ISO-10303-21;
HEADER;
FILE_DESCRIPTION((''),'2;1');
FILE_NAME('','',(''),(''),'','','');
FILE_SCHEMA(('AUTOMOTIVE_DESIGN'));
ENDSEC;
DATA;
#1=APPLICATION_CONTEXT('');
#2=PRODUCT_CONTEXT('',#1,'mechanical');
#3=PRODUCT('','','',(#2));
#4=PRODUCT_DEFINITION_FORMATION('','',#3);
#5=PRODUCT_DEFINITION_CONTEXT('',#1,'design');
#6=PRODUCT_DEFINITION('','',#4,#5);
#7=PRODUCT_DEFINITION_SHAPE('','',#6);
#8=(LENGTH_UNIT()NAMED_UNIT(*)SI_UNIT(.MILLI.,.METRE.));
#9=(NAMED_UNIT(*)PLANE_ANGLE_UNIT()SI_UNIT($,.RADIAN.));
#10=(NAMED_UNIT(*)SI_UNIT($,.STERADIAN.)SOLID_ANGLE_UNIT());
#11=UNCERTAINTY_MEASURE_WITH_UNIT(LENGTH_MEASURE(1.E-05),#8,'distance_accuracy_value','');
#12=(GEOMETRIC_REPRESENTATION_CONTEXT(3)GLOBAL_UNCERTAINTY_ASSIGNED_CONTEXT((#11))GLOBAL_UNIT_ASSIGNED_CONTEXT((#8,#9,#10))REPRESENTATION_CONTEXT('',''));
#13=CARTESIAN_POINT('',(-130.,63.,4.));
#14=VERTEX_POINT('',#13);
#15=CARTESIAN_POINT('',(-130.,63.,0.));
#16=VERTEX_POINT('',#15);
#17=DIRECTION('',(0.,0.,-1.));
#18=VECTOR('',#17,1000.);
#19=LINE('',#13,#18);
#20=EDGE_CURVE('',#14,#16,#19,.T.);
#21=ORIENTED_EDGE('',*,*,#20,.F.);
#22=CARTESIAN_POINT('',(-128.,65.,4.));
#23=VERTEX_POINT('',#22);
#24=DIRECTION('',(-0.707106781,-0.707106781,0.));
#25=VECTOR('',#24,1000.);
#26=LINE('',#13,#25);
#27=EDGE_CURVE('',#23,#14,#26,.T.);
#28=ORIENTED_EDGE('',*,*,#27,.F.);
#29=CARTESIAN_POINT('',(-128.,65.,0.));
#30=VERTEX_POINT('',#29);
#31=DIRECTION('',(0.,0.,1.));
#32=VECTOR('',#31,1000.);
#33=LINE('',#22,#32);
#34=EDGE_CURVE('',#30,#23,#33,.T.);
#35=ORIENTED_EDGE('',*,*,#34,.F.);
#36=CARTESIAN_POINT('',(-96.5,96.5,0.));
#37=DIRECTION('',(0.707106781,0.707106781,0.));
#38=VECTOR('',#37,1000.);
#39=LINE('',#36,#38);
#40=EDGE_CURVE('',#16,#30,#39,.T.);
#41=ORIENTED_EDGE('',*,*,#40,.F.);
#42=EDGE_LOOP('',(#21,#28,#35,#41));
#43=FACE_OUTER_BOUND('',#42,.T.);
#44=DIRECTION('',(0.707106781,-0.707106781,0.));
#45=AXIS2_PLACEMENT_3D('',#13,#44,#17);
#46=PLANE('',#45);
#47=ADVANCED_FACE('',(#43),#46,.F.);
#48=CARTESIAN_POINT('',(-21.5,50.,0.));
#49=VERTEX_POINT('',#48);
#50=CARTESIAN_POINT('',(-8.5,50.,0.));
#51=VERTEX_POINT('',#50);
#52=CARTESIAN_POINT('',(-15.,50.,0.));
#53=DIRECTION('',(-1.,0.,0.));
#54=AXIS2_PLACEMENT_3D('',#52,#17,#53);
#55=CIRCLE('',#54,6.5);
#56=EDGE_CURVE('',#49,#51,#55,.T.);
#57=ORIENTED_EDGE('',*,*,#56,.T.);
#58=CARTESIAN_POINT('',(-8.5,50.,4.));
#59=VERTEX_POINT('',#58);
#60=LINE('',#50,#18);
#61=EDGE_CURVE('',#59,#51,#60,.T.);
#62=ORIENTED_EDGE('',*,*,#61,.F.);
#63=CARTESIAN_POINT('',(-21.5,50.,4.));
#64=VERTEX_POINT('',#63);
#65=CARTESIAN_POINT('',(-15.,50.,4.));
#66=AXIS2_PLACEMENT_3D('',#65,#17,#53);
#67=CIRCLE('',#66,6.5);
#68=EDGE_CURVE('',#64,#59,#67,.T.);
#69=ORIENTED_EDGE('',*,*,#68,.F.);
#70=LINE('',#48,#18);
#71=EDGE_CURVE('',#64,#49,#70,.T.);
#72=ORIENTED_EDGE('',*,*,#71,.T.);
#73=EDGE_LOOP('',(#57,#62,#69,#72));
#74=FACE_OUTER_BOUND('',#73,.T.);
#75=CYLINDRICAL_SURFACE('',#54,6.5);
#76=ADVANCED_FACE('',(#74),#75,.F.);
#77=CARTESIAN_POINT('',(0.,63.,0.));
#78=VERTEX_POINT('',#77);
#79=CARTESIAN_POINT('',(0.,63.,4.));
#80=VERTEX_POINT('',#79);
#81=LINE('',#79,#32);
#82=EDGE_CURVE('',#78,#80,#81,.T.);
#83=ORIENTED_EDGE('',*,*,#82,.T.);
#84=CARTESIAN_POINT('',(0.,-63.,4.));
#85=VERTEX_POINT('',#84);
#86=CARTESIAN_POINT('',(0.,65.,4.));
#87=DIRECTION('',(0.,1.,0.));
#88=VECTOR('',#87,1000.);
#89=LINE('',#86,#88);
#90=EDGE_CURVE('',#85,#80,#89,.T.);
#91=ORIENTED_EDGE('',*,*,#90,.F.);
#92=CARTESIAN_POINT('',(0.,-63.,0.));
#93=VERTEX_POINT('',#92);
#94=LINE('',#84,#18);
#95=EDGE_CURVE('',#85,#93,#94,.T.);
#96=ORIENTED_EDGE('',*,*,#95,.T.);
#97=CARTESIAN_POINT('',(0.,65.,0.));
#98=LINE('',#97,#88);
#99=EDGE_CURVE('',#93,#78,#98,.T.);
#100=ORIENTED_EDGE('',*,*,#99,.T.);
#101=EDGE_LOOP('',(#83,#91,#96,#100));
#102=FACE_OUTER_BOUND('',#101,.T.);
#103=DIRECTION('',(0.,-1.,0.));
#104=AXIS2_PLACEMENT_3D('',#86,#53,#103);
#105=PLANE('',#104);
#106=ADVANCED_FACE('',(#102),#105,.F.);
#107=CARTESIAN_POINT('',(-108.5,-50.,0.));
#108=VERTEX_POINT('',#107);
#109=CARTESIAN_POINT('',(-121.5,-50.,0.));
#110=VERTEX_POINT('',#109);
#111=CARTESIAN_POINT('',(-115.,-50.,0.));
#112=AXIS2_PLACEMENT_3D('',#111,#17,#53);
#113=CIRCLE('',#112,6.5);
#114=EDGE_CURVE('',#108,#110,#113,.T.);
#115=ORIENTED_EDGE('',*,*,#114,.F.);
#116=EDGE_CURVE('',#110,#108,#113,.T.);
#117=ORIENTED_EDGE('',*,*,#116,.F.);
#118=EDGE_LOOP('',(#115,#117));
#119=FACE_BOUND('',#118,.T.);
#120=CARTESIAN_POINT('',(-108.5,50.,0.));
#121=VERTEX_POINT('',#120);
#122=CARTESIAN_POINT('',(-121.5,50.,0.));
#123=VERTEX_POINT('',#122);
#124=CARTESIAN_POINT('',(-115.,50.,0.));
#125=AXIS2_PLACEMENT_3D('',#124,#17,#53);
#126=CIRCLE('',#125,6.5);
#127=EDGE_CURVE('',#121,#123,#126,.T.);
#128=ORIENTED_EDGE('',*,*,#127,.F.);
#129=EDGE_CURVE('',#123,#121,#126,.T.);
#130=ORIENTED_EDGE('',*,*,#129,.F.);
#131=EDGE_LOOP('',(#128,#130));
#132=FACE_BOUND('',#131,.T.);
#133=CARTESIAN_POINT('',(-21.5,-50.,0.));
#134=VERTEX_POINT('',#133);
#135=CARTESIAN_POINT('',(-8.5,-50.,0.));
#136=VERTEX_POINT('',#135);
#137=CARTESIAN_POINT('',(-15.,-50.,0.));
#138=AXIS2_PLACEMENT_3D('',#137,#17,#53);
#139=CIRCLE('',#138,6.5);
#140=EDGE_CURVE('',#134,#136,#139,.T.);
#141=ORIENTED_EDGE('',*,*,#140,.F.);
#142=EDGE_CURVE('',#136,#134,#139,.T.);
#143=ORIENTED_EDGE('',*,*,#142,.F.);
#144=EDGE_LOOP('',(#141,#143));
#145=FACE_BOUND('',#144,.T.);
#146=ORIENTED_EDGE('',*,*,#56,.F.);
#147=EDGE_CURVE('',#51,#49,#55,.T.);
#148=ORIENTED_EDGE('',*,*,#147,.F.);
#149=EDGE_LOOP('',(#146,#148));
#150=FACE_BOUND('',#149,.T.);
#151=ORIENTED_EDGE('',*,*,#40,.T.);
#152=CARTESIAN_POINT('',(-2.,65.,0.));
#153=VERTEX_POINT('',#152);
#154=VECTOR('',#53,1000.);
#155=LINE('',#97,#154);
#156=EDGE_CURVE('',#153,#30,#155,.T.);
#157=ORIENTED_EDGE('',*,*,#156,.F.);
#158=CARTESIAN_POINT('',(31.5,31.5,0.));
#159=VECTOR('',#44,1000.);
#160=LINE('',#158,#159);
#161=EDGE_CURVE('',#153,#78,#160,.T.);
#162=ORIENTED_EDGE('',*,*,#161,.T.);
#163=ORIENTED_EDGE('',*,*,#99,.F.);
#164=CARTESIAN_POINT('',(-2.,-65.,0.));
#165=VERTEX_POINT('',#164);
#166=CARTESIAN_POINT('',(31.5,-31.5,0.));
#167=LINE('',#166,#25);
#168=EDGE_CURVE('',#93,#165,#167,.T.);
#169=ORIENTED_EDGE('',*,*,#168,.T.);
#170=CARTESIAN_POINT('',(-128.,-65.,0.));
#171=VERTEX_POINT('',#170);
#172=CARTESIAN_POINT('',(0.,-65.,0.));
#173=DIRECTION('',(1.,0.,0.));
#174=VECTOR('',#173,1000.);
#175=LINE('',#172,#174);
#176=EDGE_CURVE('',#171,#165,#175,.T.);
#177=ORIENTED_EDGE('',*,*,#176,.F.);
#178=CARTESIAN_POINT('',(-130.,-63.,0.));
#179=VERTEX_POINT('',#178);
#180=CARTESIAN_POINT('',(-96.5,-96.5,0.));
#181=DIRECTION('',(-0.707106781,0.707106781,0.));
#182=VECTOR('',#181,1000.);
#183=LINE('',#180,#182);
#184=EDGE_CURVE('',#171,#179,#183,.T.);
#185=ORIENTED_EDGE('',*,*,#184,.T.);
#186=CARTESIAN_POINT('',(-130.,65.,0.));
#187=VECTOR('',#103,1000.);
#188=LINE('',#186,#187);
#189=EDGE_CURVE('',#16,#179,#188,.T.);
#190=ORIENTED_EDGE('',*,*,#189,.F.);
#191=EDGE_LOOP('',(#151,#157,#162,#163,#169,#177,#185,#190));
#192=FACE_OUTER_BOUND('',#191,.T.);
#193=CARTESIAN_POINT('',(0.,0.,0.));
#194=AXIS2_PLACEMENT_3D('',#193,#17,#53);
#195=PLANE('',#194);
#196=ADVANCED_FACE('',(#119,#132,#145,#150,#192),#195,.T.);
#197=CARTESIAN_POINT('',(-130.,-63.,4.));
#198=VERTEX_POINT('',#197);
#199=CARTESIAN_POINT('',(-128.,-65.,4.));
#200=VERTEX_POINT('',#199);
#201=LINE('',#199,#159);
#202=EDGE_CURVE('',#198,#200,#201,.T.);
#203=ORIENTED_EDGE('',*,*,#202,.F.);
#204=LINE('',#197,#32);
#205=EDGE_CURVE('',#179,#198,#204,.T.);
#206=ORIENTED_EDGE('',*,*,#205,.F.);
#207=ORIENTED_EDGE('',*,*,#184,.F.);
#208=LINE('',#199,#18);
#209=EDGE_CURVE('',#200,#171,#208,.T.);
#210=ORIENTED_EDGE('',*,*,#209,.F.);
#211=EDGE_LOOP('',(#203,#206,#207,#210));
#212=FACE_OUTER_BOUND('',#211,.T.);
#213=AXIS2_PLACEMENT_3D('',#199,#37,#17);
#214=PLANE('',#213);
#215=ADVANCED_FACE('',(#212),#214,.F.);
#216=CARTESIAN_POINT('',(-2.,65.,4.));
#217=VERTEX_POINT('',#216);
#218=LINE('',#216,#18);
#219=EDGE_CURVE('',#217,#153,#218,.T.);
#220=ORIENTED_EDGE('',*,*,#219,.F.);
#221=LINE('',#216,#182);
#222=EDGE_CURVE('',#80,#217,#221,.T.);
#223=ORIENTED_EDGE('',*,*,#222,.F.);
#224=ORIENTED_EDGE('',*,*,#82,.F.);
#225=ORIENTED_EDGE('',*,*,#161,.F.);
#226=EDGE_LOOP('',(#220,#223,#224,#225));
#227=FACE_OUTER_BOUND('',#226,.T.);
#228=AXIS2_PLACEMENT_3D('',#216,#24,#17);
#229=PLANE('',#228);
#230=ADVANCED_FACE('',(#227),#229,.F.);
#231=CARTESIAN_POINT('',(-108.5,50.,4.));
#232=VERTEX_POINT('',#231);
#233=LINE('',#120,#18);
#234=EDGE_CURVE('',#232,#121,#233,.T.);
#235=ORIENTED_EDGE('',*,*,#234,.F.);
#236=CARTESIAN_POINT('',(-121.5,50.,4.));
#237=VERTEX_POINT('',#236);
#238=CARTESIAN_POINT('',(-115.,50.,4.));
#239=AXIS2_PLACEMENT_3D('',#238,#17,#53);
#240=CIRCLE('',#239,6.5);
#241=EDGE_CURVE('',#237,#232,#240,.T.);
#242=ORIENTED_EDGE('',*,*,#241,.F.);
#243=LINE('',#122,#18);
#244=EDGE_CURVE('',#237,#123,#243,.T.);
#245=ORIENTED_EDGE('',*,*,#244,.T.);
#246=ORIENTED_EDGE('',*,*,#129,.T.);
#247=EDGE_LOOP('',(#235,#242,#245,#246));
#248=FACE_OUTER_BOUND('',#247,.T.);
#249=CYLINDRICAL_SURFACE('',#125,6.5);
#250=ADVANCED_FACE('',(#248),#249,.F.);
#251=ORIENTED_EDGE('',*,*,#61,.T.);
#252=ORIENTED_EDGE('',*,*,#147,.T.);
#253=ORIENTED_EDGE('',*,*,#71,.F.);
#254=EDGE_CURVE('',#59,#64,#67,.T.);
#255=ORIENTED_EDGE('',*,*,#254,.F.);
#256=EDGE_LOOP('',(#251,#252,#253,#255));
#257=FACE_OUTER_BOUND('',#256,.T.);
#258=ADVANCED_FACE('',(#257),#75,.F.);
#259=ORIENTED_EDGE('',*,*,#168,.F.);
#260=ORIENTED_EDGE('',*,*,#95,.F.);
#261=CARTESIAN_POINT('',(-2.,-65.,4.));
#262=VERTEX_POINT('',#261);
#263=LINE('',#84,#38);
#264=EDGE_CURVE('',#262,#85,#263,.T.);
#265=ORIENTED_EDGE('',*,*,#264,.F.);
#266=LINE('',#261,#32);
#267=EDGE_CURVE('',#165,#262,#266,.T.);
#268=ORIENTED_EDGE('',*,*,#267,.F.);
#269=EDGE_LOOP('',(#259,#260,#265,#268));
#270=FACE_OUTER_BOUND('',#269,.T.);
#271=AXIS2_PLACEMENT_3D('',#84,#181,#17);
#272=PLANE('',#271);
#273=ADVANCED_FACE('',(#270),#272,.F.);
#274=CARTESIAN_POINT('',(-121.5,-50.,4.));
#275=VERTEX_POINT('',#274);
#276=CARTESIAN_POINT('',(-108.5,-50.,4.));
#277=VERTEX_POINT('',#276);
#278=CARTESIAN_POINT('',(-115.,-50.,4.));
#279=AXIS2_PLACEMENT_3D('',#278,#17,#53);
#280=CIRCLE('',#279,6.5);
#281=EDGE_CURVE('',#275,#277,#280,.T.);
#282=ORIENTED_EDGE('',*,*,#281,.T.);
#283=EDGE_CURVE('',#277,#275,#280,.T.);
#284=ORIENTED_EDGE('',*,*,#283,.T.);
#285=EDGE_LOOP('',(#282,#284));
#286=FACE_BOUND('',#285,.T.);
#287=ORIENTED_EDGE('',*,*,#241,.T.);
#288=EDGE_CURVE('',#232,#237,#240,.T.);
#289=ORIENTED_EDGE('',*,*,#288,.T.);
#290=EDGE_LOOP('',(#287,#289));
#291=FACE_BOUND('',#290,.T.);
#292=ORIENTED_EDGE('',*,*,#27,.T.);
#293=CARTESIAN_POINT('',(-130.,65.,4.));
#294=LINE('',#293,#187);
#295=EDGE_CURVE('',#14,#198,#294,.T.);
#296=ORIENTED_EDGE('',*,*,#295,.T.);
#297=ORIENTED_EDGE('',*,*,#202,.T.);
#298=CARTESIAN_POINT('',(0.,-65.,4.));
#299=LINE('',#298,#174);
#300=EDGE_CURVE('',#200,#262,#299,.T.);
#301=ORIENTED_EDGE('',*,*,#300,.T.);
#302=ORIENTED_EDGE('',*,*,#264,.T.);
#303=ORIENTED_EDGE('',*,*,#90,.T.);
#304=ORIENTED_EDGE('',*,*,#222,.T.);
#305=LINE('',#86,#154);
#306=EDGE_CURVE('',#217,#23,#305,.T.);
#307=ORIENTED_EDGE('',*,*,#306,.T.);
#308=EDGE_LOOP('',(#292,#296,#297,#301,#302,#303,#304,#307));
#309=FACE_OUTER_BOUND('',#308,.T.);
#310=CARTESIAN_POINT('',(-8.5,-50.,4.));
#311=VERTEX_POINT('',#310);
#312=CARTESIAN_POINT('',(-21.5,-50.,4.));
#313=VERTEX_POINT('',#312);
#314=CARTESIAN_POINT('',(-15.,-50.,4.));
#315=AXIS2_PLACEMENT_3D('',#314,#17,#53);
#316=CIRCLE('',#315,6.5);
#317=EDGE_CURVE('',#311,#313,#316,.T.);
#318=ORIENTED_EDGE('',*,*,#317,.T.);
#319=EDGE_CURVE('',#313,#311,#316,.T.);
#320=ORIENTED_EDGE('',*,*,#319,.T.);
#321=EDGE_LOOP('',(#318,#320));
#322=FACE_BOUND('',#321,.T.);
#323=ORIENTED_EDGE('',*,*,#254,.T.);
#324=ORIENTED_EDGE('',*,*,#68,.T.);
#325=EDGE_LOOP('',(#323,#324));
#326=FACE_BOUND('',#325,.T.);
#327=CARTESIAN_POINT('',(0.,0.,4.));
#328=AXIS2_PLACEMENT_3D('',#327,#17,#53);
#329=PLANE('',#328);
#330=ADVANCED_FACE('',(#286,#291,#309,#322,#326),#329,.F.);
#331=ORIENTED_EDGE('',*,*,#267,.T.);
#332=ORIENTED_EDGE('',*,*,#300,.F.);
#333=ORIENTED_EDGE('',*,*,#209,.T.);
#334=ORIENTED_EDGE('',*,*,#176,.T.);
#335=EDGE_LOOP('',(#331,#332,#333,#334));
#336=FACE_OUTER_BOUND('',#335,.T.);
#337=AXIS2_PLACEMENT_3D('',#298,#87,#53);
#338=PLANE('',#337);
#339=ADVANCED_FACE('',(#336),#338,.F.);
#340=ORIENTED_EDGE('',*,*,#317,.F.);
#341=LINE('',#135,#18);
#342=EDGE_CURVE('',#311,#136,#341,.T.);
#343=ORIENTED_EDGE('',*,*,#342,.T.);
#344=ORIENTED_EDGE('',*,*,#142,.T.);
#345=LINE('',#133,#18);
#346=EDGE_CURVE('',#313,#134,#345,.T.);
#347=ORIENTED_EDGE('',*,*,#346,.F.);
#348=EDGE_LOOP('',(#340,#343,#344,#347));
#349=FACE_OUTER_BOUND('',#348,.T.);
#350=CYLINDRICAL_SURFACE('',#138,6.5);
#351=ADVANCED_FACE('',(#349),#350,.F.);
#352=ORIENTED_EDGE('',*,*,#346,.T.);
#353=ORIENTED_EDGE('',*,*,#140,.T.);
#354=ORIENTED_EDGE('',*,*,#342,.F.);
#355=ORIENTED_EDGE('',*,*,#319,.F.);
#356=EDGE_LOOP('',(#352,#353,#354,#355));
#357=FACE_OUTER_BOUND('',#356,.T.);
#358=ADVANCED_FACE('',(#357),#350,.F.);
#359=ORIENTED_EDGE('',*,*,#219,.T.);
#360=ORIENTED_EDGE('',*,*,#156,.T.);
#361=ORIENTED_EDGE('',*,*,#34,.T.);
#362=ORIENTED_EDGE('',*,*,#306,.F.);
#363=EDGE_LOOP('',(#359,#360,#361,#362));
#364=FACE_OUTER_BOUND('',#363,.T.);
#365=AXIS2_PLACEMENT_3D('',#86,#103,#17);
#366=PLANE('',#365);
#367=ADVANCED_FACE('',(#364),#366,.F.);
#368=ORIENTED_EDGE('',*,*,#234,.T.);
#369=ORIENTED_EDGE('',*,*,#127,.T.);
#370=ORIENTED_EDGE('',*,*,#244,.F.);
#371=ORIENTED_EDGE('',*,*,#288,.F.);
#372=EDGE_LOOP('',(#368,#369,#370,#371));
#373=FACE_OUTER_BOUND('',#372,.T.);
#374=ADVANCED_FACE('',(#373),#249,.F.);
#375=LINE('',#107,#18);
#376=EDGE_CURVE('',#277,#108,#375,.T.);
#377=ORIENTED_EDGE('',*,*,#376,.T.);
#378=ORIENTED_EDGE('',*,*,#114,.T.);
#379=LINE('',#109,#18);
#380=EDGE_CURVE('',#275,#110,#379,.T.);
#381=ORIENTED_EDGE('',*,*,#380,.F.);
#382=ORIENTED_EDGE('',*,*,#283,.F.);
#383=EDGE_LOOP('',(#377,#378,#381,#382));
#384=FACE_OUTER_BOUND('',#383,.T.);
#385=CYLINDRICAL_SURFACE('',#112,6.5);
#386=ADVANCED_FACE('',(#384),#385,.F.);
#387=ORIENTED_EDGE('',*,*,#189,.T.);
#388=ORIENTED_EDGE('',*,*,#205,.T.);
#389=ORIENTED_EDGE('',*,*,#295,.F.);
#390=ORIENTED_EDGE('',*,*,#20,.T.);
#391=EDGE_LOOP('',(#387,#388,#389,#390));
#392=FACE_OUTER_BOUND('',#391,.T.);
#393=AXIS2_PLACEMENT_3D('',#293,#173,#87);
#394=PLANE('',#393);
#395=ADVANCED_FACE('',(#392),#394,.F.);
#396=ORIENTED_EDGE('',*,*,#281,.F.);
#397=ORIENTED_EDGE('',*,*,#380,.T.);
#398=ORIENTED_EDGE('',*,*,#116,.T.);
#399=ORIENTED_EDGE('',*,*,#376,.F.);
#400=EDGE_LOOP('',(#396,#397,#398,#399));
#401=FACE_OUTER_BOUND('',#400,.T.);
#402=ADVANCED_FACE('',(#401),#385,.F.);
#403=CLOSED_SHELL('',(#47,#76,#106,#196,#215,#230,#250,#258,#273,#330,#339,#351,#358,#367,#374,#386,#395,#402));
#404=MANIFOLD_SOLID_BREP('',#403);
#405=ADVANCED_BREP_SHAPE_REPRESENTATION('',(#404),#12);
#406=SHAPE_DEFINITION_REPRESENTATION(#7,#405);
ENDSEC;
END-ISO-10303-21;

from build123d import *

# Parameters (mm, degrees)
SKETCH_1_W              = 130
SKETCH_1_H              = 130
EXTRUDE_1_DEPTH         = 4
CHAMFER_1_SIZE          = 2
HOLE_WIZARD_13_0_13_1_D = 13


with BuildPart() as part:
    # 草图1 → 凸台-拉伸1 (new body)
    with BuildSketch(Plane.XY):
        with Locations((-65, 0)):
            Rectangle(SKETCH_1_W, SKETCH_1_H)
    extrude(amount=EXTRUDE_1_DEPTH)

    # 倒角1
    chamfer_1_edges = [part.edges().sort_by_distance(p)[0] for p in [
        (0, -65, 2),
        (-130, -65, 2),
        (-130, 65, 2),
        (0, 65, 2),
    ]]
    chamfer(chamfer_1_edges, length=CHAMFER_1_SIZE)

    # Ø13.0 (13) 直径孔1 (through all)
    with Locations(Plane(origin=(0, 0, 0), x_dir=(-1, 0, 0), z_dir=(0, 0, -1))):
        with Locations((15, -50), (15, 50), (115, -50), (115, 50)):
            Hole(HOLE_WIZARD_13_0_13_1_D / 2)


solid = part.part
